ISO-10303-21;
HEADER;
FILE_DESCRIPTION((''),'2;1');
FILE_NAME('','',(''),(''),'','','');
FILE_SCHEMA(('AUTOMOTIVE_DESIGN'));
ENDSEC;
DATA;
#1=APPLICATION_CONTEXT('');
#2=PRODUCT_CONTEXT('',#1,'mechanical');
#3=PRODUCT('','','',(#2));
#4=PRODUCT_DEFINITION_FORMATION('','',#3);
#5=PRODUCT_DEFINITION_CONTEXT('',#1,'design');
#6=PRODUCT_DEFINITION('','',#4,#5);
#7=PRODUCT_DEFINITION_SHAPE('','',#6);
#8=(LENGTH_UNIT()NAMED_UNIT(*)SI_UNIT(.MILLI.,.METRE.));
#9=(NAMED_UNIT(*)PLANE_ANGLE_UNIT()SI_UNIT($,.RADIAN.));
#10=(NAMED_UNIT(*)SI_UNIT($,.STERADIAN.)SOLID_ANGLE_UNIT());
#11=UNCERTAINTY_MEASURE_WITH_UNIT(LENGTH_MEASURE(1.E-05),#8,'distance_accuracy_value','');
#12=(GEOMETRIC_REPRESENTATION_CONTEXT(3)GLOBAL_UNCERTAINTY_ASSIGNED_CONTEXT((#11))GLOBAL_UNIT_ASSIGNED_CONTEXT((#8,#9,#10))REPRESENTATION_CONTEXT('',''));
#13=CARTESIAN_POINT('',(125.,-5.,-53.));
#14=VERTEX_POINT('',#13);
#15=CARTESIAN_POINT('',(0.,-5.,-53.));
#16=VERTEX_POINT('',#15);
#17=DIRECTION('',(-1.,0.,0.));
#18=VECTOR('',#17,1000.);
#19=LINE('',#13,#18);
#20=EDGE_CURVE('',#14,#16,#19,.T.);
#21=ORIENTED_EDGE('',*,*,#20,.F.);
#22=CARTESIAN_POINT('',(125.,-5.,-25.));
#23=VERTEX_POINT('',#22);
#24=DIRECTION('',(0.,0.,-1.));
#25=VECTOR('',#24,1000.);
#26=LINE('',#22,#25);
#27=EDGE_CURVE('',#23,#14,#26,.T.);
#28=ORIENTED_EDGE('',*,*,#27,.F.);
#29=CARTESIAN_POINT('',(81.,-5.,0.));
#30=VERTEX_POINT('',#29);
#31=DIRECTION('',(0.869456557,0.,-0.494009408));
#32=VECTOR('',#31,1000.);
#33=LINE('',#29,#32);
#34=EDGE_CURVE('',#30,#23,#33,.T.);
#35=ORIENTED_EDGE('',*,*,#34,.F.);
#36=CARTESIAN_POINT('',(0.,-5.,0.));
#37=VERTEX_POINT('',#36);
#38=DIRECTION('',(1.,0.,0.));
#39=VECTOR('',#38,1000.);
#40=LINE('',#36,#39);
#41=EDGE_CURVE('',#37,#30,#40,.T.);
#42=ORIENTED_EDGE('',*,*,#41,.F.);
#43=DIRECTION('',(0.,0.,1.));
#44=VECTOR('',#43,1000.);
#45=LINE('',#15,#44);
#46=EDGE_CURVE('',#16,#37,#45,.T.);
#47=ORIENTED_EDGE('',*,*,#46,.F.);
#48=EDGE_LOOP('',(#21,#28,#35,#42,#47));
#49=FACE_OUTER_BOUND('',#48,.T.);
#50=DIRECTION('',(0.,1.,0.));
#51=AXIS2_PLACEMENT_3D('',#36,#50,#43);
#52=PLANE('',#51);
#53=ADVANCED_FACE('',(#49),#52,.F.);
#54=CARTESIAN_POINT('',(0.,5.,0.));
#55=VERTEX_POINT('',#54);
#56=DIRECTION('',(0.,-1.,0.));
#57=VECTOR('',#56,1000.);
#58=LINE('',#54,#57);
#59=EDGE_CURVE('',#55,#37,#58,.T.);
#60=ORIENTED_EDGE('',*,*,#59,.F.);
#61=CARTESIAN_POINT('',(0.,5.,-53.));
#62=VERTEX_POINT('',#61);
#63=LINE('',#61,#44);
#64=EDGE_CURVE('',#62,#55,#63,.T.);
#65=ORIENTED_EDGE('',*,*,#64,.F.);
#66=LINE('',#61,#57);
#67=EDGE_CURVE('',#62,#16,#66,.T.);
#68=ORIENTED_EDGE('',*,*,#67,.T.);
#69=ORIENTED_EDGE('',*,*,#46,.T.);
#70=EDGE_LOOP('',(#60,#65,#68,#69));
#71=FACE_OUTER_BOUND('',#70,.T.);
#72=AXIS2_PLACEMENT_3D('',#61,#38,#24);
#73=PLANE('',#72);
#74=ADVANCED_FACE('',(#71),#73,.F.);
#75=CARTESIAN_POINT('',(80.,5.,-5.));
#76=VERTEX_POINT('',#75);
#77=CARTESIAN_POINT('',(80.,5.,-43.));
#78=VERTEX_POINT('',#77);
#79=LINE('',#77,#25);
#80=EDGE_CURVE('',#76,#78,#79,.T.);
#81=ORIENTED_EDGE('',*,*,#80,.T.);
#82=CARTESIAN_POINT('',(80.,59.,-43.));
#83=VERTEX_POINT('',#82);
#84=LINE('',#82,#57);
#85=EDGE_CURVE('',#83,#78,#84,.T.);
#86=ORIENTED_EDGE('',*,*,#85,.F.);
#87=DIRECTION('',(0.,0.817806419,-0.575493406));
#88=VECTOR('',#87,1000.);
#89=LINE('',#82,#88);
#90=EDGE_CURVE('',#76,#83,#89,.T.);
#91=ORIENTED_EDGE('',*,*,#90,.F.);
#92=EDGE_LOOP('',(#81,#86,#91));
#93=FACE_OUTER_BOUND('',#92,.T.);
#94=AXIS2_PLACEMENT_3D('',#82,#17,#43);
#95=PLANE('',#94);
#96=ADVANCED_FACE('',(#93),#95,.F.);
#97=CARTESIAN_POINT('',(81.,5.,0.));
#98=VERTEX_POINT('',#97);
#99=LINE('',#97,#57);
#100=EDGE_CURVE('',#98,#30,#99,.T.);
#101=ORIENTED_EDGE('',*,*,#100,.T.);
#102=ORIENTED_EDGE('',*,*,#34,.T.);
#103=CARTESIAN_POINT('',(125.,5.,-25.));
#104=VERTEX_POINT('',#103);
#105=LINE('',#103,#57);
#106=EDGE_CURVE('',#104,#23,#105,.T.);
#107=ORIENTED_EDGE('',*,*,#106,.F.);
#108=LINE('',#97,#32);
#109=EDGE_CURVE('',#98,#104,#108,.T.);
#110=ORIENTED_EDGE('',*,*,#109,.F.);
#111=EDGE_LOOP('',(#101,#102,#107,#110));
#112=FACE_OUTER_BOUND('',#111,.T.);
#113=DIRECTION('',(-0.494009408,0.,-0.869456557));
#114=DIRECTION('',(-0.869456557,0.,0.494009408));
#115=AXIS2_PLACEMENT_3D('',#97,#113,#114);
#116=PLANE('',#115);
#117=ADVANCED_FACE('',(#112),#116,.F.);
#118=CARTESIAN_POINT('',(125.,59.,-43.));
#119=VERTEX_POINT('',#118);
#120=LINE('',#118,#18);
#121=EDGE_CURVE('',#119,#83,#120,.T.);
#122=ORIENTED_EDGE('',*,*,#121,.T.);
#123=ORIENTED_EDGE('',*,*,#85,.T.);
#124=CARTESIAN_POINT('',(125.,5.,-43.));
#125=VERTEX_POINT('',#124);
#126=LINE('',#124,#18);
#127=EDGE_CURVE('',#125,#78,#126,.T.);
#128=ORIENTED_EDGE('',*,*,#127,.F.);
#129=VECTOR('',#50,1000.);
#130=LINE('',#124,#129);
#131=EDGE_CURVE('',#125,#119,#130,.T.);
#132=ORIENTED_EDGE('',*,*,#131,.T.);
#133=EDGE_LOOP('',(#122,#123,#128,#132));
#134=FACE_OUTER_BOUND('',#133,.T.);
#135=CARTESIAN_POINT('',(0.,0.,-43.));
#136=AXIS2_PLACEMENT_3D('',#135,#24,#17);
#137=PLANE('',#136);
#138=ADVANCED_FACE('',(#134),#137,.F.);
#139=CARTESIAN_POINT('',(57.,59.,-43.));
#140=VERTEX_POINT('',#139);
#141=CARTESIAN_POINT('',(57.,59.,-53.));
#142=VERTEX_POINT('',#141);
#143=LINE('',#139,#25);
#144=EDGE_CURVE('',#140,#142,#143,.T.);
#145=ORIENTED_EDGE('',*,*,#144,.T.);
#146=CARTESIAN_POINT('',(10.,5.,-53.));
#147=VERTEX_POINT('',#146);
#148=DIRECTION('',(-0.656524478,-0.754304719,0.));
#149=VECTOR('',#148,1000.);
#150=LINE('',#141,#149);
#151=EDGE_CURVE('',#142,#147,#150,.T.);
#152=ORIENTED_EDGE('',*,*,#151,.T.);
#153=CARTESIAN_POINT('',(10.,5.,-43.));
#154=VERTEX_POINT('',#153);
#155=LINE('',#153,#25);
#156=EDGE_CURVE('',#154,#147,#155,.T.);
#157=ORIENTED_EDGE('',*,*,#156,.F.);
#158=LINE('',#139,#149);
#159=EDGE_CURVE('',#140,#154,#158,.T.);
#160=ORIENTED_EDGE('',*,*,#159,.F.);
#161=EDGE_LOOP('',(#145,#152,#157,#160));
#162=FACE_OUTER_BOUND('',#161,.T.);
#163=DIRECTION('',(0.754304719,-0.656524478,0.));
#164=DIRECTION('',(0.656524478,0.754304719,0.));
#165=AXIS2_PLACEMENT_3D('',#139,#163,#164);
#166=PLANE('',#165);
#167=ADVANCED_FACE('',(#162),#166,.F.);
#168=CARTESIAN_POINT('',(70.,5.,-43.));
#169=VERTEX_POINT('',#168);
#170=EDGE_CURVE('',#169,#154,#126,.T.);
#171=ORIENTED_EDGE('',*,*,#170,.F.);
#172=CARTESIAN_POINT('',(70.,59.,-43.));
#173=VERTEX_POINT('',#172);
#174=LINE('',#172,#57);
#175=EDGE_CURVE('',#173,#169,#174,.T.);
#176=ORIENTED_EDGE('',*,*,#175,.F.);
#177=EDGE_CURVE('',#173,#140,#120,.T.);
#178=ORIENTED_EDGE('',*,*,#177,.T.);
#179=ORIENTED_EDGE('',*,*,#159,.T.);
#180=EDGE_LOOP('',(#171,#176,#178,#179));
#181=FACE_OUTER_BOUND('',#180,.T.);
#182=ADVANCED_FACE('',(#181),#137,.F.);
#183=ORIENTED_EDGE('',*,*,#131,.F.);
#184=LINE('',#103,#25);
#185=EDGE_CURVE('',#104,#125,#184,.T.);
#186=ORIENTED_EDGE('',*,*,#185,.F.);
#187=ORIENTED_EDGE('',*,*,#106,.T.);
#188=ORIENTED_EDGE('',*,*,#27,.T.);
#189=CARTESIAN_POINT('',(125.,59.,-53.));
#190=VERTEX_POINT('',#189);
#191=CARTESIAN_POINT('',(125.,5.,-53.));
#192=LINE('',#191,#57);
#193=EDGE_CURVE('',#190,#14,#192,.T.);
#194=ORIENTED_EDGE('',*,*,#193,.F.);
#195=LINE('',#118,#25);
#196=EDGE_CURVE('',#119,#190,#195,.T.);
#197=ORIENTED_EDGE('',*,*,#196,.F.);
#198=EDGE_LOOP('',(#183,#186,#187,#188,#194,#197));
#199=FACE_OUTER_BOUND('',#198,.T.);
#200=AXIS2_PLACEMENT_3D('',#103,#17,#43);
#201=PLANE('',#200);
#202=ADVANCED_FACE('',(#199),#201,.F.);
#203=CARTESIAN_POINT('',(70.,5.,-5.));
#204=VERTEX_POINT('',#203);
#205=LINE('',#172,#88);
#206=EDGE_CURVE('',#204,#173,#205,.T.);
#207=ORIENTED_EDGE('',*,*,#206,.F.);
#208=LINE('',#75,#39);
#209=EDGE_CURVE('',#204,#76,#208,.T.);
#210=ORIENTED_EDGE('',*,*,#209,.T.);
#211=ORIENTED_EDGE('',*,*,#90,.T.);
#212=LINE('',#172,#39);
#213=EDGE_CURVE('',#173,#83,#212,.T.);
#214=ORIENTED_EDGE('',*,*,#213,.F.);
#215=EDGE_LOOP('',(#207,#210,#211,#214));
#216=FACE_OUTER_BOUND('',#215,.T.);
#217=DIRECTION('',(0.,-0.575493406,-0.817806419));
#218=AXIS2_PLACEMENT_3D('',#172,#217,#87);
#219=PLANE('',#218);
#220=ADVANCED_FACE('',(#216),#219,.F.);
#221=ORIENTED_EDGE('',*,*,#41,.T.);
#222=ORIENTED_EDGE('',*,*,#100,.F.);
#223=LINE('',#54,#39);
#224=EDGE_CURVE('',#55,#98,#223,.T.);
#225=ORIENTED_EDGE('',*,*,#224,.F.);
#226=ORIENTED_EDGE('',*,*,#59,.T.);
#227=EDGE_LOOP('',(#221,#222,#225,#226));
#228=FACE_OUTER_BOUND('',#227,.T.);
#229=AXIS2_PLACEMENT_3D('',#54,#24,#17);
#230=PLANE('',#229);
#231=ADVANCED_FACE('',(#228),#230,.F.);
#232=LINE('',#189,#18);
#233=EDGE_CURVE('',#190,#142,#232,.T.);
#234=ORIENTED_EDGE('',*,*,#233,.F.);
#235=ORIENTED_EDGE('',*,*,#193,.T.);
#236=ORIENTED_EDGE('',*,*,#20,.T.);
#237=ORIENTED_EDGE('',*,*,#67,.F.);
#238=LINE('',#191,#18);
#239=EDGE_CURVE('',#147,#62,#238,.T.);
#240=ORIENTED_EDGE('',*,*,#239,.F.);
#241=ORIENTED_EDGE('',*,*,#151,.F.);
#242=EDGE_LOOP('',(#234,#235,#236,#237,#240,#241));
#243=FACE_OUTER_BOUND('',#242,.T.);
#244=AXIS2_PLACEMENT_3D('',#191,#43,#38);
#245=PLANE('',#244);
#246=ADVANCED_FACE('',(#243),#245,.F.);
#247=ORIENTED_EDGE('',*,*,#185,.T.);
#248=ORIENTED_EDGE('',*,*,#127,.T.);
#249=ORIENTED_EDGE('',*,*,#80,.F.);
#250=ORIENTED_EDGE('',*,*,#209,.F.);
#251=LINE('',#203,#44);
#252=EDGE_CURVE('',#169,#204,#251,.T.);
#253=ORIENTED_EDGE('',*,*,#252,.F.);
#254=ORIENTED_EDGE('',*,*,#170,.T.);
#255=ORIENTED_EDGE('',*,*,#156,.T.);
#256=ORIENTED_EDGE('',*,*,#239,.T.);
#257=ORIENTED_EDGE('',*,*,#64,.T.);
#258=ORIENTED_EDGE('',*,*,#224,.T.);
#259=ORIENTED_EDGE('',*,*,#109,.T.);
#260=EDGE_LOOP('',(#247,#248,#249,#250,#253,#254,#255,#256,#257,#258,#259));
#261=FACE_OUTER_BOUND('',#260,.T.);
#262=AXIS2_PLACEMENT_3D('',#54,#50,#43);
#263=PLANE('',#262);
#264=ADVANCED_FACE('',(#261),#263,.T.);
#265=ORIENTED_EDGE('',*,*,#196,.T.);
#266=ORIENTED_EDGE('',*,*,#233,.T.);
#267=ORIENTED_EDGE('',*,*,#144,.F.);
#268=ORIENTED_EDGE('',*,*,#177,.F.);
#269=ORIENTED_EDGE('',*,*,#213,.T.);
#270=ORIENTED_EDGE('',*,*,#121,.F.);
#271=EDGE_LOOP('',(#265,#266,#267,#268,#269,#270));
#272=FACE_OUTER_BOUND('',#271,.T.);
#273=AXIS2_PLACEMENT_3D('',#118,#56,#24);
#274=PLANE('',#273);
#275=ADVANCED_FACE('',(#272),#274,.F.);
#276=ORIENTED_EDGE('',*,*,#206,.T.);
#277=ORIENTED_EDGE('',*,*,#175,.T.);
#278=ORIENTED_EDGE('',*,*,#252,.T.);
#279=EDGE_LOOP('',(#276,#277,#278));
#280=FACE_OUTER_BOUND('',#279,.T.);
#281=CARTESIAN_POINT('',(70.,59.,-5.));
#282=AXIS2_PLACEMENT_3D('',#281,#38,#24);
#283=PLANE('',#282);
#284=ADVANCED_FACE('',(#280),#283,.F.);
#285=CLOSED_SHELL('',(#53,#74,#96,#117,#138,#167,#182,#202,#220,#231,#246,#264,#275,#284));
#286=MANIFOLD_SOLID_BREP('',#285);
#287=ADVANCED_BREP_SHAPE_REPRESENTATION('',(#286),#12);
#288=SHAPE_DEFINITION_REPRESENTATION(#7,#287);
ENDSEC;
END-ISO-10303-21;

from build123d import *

# Parameters (mm, degrees)
BASE_PLATE_DEPTH       = 5
RAISED_PAD_DEPTH       = 10
UPRIGHT_WALL_PROFILE_W = 10
UPRIGHT_WALL_PROFILE_H = 38
UPRIGHT_WALL_DEPTH     = 54
GUSSET_CUT_DEPTH       = 10


with BuildPart() as part:
    # Base Plate Profile → Base Plate (new, symmetric)
    with BuildSketch(Plane(origin=(0, 0, 0), x_dir=(1, 0, 0), z_dir=(0, 1, 0))):
        Polygon((0, 0), (81, 0), (125, 25), (125, 53), (0, 53), align=None)
    extrude(amount=BASE_PLATE_DEPTH, both=True)

    # Raised Pad Profile → Raised Pad (add)
    with BuildSketch(Plane(origin=(0, 0, -53), x_dir=(-1, 0, 0), z_dir=(0, 0, -1))):
        Polygon((-125, 5), (-10, 5), (-57, 59), (-125, 59), align=None)
    extrude(amount=-RAISED_PAD_DEPTH)

    # Upright Wall Profile → Upright Wall (add)
    with BuildSketch(Plane(origin=(0, 5, 0), x_dir=(1, 0, 0), z_dir=(0, 1, 0))):
        with Locations((75, 24)):
            Rectangle(UPRIGHT_WALL_PROFILE_W, UPRIGHT_WALL_PROFILE_H)
    extrude(amount=UPRIGHT_WALL_DEPTH)

    # Gusset Cut Profile → Gusset Cut (cut)
    with BuildSketch(Plane(origin=(80, 0, 0), x_dir=(0, 0, -1), z_dir=(1, 0, 0))):
        Polygon((43, 59), (5, 5), (5, 59), align=None)
    extrude(amount=-GUSSET_CUT_DEPTH, mode=Mode.SUBTRACT)


solid = part.part
